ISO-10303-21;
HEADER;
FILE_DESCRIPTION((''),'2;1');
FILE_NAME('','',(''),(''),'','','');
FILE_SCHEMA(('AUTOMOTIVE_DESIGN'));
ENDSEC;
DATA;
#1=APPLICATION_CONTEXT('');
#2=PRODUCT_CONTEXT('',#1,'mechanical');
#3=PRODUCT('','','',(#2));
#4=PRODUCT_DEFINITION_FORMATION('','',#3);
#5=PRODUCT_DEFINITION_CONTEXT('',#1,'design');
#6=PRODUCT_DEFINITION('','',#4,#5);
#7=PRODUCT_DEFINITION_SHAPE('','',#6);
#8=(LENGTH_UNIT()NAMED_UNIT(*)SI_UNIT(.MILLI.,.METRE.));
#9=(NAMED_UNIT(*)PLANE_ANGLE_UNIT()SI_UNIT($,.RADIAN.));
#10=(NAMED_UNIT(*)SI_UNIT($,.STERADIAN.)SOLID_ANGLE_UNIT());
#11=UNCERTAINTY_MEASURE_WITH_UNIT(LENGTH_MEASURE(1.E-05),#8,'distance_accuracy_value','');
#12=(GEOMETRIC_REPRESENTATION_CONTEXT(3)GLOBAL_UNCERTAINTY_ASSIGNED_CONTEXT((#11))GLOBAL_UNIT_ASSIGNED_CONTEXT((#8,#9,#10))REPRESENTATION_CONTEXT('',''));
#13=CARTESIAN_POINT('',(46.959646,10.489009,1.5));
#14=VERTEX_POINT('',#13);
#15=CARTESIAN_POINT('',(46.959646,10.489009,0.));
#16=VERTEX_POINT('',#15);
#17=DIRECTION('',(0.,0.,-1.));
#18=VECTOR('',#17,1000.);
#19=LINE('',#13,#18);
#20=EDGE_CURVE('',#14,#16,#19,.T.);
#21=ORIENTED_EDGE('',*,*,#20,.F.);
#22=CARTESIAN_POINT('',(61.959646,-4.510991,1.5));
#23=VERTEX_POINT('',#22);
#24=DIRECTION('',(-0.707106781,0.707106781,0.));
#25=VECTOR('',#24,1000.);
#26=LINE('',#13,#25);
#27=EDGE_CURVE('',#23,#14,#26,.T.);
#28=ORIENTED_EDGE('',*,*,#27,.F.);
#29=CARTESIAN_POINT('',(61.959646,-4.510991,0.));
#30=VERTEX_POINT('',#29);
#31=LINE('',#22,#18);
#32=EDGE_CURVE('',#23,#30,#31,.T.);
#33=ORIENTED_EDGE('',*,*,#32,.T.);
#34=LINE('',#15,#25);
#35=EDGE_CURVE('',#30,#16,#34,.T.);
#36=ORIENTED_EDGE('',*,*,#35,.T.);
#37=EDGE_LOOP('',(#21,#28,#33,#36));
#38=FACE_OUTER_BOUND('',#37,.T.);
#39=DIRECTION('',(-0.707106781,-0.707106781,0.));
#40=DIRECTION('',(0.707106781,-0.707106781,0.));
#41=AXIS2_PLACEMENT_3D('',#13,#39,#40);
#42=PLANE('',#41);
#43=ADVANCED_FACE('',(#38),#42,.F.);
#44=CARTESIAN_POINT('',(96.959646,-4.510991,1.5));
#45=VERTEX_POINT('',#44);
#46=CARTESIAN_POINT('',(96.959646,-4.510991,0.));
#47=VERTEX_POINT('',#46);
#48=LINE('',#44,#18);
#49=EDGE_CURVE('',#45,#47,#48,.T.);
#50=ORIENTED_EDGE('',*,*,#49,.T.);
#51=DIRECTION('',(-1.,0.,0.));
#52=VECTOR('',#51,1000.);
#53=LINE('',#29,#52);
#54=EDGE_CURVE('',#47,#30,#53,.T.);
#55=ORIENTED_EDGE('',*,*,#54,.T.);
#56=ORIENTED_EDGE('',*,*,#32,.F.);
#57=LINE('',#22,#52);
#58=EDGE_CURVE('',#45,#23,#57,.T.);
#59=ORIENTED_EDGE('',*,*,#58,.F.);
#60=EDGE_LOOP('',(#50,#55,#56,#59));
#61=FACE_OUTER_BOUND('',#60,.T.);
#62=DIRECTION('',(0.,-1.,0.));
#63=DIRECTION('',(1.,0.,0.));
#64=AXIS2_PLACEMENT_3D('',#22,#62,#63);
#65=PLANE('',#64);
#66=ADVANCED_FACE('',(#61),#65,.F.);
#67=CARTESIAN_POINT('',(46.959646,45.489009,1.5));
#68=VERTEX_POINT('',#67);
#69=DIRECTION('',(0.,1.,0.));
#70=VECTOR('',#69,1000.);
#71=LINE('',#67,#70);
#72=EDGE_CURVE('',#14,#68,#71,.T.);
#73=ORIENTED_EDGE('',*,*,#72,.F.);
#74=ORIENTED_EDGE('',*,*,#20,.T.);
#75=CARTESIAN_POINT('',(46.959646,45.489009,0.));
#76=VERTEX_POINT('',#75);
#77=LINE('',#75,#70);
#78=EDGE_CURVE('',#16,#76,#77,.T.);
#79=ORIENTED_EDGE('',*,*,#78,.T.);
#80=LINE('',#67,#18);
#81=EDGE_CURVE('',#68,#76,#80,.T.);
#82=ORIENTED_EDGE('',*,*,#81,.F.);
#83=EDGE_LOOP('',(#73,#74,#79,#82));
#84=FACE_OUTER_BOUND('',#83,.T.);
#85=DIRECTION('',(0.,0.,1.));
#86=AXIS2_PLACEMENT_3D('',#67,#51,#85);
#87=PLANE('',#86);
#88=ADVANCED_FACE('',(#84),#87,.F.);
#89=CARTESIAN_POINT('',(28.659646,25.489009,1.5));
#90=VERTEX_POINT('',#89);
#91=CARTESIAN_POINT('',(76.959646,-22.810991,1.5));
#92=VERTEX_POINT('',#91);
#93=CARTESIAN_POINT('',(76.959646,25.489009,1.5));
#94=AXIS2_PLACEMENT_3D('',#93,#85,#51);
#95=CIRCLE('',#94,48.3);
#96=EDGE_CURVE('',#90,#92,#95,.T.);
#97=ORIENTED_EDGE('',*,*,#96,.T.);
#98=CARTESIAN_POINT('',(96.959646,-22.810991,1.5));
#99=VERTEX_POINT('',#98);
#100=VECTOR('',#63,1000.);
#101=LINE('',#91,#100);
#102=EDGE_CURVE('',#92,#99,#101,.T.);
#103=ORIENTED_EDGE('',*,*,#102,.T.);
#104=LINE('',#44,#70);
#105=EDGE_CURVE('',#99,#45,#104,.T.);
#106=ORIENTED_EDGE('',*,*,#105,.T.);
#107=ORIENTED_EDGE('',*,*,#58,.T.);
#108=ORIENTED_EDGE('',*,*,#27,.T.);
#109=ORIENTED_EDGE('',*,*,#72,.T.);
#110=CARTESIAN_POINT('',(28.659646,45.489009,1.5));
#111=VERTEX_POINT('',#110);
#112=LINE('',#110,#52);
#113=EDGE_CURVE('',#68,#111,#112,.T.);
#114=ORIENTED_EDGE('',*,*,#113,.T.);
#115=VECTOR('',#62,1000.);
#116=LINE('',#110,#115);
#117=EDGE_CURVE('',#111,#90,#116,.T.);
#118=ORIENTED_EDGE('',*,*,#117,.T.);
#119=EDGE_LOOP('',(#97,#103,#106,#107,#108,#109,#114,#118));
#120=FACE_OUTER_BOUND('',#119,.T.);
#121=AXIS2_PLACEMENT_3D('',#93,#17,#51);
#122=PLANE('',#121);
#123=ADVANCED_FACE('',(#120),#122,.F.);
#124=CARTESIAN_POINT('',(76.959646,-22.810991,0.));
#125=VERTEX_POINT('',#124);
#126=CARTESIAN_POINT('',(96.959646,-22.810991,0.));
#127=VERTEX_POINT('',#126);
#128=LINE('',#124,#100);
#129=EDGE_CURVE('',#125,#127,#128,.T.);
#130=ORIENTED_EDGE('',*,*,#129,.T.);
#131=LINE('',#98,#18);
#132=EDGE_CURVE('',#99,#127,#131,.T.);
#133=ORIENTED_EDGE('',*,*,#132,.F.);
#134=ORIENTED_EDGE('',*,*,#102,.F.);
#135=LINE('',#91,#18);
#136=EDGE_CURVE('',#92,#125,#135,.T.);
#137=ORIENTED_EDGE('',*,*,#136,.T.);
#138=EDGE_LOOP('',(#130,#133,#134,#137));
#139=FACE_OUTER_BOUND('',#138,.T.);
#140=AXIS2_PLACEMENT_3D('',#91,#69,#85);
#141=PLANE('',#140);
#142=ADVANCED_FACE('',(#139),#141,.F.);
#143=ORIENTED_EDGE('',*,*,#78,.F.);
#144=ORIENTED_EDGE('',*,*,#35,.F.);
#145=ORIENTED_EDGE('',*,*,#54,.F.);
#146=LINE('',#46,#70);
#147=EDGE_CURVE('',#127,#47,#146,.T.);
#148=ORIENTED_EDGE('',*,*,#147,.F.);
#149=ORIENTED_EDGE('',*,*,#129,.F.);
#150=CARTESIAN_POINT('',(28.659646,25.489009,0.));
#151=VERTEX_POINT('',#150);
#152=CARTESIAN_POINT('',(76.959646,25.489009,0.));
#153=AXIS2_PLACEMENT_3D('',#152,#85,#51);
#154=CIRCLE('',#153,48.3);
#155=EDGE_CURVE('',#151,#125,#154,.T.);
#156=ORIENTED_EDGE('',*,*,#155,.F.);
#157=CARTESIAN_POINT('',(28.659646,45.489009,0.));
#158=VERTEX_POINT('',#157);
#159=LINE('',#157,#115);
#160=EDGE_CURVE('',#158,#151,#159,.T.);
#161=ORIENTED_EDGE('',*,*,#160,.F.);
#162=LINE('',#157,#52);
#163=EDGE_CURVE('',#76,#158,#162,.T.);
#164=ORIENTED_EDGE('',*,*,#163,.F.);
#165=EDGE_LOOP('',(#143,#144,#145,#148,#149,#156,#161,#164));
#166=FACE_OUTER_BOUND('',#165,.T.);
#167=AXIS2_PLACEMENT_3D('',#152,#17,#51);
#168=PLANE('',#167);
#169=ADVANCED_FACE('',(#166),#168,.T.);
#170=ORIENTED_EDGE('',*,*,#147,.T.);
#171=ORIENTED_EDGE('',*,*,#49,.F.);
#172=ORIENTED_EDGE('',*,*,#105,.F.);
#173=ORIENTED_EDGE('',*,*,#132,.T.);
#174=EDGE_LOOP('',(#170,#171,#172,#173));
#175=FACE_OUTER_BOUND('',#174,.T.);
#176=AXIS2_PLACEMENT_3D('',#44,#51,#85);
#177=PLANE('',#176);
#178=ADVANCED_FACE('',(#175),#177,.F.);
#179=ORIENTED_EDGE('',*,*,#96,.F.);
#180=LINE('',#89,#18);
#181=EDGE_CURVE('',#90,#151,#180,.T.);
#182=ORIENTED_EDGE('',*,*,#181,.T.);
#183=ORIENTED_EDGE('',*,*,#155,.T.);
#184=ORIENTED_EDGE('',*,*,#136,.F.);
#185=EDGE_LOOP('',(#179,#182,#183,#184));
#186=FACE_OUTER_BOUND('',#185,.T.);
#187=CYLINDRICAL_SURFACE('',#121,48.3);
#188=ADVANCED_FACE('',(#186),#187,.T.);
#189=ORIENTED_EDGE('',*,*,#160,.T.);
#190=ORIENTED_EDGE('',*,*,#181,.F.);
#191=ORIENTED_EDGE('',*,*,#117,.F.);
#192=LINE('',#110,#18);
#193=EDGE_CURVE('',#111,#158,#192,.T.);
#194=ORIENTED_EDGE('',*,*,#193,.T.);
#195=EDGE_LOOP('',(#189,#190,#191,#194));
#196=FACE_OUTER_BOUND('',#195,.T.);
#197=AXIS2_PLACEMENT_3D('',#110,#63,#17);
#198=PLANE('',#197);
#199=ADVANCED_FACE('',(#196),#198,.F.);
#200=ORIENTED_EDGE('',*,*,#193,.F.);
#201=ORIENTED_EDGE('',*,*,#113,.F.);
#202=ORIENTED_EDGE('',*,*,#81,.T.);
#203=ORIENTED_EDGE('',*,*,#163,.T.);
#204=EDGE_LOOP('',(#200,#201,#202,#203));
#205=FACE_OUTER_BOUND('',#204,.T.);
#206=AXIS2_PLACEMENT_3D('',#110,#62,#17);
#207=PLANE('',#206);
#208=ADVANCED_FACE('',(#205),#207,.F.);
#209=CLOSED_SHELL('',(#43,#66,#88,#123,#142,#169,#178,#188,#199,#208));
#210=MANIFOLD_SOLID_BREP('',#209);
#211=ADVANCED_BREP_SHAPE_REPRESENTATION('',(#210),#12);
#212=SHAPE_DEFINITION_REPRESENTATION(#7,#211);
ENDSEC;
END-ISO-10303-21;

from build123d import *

# Parameters (mm, degrees)
EXTRUDE_1_DEPTH = 1.5


with BuildPart() as part:
    # 草图1 → 凸台-拉伸1 (new body)
    with BuildSketch(Plane.XY):
        with BuildLine():
            Line((28.659646302, 45.489008558), (28.659646302, 25.489008558))
            ThreePointArc((28.659646302, 25.489008558), (42.806388771, -8.664248973), (76.959646302, -22.810991442))
            Line((76.959646302, -22.810991442), (96.959646302, -22.810991442))
            Line((96.959646302, -22.810991442), (96.959646302, -4.510991442))
            Line((96.959646302, -4.510991442), (61.959646302, -4.510991442))
            Line((61.959646302, -4.510991442), (46.959646302, 10.489008558))
            Line((46.959646302, 10.489008558), (46.959646302, 45.489008558))
            Line((46.959646302, 45.489008558), (28.659646302, 45.489008558))
        make_face()
    extrude(amount=EXTRUDE_1_DEPTH)


solid = part.part
